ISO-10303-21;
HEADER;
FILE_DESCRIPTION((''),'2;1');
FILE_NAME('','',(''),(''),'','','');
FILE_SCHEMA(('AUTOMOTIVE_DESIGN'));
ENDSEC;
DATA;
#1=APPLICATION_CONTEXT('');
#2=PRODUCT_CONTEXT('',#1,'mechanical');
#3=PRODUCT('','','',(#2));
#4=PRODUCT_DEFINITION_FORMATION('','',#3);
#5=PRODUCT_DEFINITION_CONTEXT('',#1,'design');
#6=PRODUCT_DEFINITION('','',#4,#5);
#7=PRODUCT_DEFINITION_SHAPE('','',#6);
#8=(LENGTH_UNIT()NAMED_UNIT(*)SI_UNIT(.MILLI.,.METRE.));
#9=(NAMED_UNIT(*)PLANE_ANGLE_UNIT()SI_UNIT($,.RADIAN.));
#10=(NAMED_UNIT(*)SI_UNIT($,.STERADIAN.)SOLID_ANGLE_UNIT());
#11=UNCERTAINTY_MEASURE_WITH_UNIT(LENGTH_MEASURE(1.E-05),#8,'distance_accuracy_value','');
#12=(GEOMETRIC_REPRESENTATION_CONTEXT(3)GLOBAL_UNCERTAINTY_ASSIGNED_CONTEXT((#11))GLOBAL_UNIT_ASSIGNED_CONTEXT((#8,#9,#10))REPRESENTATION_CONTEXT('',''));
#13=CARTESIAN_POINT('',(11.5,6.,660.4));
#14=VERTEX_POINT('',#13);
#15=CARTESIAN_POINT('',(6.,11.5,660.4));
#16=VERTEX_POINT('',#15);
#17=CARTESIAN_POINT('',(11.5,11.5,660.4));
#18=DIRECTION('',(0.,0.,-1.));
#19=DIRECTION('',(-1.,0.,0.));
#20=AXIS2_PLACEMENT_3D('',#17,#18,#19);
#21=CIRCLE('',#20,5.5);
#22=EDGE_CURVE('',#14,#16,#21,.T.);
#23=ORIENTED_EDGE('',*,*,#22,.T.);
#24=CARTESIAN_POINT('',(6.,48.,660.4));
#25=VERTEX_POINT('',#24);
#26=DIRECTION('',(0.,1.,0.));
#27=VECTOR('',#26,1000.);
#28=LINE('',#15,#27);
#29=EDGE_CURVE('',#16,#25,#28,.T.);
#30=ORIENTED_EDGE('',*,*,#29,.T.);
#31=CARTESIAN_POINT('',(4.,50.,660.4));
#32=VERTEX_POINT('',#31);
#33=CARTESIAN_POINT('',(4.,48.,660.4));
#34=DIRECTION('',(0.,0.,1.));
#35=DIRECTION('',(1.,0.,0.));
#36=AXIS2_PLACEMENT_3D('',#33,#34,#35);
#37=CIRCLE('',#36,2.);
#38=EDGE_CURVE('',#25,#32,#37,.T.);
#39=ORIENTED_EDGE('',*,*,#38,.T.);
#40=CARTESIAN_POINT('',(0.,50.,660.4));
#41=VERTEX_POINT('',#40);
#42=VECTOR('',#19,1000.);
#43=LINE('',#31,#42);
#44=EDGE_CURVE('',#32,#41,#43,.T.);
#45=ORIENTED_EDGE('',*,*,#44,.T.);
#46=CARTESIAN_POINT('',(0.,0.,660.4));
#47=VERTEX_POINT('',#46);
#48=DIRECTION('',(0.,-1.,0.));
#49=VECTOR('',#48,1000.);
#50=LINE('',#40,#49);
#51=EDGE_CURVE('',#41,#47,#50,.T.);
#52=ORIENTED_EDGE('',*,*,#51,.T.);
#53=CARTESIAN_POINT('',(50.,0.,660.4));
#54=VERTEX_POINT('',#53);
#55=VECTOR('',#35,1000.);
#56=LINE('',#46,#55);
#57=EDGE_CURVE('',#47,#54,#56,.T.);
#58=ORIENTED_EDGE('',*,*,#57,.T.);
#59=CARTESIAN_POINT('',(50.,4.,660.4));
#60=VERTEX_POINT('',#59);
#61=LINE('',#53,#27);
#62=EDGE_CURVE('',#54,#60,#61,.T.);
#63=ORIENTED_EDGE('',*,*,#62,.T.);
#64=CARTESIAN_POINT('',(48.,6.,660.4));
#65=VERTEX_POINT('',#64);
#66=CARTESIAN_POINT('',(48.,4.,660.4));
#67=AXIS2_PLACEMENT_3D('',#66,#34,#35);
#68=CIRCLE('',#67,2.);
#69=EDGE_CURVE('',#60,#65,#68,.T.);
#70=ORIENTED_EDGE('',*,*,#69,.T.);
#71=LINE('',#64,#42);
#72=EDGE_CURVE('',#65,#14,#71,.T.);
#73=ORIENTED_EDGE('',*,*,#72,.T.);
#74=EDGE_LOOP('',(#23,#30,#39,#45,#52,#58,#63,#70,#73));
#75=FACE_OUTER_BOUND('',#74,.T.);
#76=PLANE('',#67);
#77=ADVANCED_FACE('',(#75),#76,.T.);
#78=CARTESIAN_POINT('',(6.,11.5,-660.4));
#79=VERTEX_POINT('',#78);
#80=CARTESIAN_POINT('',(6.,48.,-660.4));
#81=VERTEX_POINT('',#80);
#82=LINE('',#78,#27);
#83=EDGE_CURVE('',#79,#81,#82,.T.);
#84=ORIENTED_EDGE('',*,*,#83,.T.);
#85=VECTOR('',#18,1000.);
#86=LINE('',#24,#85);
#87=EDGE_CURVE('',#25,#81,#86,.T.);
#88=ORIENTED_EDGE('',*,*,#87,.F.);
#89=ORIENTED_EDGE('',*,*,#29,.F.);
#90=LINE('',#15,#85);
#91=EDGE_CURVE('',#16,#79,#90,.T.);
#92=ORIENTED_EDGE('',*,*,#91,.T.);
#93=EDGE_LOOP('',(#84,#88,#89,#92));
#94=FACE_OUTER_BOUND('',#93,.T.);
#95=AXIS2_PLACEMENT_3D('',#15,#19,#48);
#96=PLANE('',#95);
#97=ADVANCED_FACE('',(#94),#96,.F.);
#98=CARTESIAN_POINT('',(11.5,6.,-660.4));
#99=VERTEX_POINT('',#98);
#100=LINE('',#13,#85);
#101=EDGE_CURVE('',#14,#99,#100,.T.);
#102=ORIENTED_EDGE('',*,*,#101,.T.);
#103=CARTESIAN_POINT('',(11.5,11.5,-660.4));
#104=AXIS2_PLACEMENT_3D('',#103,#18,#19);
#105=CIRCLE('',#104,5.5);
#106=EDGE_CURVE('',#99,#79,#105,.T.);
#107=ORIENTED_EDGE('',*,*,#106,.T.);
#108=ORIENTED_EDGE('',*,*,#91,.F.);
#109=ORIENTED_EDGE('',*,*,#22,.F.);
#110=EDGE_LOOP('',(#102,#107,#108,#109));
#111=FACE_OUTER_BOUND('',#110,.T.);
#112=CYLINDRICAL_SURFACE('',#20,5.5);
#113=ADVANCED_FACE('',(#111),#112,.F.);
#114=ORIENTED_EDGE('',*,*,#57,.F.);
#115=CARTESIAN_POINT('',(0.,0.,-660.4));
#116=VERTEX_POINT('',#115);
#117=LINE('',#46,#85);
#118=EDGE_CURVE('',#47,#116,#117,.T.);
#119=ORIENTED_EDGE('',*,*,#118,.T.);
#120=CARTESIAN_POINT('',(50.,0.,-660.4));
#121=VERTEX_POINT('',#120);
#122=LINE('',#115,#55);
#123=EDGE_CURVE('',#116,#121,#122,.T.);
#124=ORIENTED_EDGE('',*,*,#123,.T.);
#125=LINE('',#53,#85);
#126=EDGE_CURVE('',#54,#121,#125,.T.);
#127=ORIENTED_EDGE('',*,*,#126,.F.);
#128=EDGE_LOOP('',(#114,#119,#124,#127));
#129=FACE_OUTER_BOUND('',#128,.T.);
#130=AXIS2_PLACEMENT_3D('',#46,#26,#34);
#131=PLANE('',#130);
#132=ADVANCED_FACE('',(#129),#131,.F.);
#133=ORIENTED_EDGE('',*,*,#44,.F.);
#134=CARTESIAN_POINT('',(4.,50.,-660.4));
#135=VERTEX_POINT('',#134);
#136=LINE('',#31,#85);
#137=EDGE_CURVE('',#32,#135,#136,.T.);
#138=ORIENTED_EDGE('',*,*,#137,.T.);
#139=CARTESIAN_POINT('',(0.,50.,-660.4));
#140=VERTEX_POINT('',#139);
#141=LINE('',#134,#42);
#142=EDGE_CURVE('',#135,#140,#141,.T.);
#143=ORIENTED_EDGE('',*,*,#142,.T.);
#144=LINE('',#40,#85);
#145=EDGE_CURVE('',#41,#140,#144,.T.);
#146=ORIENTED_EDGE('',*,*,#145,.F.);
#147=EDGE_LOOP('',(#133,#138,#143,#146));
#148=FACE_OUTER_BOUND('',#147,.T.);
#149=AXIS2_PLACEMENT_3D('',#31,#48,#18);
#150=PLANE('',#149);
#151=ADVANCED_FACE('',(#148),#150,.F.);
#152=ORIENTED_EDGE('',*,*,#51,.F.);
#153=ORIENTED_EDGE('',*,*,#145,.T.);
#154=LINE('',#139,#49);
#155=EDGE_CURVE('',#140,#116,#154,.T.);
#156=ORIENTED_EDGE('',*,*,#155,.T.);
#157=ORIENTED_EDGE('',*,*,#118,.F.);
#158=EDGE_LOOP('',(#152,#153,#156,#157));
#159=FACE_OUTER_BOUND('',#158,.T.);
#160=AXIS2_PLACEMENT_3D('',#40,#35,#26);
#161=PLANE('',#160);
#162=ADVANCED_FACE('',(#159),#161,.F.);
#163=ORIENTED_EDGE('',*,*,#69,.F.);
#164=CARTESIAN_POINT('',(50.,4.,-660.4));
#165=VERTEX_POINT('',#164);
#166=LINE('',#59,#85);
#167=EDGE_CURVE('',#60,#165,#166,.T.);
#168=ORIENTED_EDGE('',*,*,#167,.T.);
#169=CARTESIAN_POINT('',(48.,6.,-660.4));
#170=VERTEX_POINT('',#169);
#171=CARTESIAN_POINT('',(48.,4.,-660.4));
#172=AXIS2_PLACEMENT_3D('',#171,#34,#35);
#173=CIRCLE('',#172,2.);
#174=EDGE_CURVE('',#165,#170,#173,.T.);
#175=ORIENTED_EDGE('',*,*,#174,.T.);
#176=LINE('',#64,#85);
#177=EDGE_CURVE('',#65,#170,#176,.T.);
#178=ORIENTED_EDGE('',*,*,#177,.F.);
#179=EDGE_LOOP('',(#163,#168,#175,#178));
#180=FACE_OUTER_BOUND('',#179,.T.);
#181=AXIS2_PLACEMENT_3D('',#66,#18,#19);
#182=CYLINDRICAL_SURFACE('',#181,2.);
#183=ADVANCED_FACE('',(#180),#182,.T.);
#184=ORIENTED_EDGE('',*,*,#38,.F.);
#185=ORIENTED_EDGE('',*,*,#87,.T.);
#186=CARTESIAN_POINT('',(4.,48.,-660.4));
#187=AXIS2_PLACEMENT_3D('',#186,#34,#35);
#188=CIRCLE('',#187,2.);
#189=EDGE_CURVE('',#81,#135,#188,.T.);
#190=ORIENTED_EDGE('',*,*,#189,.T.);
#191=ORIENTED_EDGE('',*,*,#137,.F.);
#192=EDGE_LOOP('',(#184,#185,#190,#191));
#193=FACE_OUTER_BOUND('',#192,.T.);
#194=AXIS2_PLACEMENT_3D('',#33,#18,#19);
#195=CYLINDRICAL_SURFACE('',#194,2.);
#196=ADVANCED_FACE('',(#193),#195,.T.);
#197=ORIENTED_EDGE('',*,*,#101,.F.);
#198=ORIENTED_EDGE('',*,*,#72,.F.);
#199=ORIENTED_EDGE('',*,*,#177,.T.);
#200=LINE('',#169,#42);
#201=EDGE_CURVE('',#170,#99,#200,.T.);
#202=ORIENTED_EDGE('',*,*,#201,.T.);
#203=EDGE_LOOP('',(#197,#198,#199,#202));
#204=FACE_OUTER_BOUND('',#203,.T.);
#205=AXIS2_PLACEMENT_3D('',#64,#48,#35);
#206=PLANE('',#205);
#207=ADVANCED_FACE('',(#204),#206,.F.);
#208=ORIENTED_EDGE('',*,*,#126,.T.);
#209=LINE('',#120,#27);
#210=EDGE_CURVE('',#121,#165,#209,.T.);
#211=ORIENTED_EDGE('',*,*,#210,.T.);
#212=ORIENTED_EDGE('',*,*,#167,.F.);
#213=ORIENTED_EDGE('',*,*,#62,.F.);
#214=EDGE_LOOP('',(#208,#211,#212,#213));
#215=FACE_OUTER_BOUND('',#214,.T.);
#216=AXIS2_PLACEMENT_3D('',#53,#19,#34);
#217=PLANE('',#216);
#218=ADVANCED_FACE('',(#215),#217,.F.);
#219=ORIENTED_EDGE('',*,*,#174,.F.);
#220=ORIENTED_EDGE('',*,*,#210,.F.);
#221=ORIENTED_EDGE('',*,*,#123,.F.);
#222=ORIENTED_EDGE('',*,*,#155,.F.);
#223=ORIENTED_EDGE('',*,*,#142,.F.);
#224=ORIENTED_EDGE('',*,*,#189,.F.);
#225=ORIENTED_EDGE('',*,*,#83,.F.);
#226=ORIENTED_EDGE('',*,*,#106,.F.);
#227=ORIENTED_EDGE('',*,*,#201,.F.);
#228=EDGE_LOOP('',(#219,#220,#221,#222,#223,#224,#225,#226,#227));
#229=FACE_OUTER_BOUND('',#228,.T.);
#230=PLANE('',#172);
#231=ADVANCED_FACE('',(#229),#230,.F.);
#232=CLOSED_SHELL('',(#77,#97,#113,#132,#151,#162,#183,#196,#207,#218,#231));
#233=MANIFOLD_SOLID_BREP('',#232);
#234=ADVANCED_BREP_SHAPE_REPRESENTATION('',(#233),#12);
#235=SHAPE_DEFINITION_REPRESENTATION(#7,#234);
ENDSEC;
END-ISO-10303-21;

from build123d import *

# Parameters (mm, degrees)
BOSS_EXTRUDE1_DEPTH = 660.4


with BuildPart() as part:
    # Sketch1 → Boss-Extrude1 (new, symmetric)
    with BuildSketch(Plane.XY):
        with BuildLine():
            Line((0, 50), (0, 0))
            Line((0, 0), (50, 0))
            Line((50, 0), (50, 4))
            ThreePointArc((50, 4), (49.414213562, 5.414213562), (48, 6))
            Line((48, 6), (11.5, 6))
            ThreePointArc((11.5, 6), (7.610912703, 7.610912703), (6, 11.5))
            Line((6, 11.5), (6, 48))
            ThreePointArc((6, 48), (5.414213562, 49.414213562), (4, 50))
            Line((4, 50), (0, 50))
        make_face()
    extrude(amount=BOSS_EXTRUDE1_DEPTH, both=True)


solid = part.part
